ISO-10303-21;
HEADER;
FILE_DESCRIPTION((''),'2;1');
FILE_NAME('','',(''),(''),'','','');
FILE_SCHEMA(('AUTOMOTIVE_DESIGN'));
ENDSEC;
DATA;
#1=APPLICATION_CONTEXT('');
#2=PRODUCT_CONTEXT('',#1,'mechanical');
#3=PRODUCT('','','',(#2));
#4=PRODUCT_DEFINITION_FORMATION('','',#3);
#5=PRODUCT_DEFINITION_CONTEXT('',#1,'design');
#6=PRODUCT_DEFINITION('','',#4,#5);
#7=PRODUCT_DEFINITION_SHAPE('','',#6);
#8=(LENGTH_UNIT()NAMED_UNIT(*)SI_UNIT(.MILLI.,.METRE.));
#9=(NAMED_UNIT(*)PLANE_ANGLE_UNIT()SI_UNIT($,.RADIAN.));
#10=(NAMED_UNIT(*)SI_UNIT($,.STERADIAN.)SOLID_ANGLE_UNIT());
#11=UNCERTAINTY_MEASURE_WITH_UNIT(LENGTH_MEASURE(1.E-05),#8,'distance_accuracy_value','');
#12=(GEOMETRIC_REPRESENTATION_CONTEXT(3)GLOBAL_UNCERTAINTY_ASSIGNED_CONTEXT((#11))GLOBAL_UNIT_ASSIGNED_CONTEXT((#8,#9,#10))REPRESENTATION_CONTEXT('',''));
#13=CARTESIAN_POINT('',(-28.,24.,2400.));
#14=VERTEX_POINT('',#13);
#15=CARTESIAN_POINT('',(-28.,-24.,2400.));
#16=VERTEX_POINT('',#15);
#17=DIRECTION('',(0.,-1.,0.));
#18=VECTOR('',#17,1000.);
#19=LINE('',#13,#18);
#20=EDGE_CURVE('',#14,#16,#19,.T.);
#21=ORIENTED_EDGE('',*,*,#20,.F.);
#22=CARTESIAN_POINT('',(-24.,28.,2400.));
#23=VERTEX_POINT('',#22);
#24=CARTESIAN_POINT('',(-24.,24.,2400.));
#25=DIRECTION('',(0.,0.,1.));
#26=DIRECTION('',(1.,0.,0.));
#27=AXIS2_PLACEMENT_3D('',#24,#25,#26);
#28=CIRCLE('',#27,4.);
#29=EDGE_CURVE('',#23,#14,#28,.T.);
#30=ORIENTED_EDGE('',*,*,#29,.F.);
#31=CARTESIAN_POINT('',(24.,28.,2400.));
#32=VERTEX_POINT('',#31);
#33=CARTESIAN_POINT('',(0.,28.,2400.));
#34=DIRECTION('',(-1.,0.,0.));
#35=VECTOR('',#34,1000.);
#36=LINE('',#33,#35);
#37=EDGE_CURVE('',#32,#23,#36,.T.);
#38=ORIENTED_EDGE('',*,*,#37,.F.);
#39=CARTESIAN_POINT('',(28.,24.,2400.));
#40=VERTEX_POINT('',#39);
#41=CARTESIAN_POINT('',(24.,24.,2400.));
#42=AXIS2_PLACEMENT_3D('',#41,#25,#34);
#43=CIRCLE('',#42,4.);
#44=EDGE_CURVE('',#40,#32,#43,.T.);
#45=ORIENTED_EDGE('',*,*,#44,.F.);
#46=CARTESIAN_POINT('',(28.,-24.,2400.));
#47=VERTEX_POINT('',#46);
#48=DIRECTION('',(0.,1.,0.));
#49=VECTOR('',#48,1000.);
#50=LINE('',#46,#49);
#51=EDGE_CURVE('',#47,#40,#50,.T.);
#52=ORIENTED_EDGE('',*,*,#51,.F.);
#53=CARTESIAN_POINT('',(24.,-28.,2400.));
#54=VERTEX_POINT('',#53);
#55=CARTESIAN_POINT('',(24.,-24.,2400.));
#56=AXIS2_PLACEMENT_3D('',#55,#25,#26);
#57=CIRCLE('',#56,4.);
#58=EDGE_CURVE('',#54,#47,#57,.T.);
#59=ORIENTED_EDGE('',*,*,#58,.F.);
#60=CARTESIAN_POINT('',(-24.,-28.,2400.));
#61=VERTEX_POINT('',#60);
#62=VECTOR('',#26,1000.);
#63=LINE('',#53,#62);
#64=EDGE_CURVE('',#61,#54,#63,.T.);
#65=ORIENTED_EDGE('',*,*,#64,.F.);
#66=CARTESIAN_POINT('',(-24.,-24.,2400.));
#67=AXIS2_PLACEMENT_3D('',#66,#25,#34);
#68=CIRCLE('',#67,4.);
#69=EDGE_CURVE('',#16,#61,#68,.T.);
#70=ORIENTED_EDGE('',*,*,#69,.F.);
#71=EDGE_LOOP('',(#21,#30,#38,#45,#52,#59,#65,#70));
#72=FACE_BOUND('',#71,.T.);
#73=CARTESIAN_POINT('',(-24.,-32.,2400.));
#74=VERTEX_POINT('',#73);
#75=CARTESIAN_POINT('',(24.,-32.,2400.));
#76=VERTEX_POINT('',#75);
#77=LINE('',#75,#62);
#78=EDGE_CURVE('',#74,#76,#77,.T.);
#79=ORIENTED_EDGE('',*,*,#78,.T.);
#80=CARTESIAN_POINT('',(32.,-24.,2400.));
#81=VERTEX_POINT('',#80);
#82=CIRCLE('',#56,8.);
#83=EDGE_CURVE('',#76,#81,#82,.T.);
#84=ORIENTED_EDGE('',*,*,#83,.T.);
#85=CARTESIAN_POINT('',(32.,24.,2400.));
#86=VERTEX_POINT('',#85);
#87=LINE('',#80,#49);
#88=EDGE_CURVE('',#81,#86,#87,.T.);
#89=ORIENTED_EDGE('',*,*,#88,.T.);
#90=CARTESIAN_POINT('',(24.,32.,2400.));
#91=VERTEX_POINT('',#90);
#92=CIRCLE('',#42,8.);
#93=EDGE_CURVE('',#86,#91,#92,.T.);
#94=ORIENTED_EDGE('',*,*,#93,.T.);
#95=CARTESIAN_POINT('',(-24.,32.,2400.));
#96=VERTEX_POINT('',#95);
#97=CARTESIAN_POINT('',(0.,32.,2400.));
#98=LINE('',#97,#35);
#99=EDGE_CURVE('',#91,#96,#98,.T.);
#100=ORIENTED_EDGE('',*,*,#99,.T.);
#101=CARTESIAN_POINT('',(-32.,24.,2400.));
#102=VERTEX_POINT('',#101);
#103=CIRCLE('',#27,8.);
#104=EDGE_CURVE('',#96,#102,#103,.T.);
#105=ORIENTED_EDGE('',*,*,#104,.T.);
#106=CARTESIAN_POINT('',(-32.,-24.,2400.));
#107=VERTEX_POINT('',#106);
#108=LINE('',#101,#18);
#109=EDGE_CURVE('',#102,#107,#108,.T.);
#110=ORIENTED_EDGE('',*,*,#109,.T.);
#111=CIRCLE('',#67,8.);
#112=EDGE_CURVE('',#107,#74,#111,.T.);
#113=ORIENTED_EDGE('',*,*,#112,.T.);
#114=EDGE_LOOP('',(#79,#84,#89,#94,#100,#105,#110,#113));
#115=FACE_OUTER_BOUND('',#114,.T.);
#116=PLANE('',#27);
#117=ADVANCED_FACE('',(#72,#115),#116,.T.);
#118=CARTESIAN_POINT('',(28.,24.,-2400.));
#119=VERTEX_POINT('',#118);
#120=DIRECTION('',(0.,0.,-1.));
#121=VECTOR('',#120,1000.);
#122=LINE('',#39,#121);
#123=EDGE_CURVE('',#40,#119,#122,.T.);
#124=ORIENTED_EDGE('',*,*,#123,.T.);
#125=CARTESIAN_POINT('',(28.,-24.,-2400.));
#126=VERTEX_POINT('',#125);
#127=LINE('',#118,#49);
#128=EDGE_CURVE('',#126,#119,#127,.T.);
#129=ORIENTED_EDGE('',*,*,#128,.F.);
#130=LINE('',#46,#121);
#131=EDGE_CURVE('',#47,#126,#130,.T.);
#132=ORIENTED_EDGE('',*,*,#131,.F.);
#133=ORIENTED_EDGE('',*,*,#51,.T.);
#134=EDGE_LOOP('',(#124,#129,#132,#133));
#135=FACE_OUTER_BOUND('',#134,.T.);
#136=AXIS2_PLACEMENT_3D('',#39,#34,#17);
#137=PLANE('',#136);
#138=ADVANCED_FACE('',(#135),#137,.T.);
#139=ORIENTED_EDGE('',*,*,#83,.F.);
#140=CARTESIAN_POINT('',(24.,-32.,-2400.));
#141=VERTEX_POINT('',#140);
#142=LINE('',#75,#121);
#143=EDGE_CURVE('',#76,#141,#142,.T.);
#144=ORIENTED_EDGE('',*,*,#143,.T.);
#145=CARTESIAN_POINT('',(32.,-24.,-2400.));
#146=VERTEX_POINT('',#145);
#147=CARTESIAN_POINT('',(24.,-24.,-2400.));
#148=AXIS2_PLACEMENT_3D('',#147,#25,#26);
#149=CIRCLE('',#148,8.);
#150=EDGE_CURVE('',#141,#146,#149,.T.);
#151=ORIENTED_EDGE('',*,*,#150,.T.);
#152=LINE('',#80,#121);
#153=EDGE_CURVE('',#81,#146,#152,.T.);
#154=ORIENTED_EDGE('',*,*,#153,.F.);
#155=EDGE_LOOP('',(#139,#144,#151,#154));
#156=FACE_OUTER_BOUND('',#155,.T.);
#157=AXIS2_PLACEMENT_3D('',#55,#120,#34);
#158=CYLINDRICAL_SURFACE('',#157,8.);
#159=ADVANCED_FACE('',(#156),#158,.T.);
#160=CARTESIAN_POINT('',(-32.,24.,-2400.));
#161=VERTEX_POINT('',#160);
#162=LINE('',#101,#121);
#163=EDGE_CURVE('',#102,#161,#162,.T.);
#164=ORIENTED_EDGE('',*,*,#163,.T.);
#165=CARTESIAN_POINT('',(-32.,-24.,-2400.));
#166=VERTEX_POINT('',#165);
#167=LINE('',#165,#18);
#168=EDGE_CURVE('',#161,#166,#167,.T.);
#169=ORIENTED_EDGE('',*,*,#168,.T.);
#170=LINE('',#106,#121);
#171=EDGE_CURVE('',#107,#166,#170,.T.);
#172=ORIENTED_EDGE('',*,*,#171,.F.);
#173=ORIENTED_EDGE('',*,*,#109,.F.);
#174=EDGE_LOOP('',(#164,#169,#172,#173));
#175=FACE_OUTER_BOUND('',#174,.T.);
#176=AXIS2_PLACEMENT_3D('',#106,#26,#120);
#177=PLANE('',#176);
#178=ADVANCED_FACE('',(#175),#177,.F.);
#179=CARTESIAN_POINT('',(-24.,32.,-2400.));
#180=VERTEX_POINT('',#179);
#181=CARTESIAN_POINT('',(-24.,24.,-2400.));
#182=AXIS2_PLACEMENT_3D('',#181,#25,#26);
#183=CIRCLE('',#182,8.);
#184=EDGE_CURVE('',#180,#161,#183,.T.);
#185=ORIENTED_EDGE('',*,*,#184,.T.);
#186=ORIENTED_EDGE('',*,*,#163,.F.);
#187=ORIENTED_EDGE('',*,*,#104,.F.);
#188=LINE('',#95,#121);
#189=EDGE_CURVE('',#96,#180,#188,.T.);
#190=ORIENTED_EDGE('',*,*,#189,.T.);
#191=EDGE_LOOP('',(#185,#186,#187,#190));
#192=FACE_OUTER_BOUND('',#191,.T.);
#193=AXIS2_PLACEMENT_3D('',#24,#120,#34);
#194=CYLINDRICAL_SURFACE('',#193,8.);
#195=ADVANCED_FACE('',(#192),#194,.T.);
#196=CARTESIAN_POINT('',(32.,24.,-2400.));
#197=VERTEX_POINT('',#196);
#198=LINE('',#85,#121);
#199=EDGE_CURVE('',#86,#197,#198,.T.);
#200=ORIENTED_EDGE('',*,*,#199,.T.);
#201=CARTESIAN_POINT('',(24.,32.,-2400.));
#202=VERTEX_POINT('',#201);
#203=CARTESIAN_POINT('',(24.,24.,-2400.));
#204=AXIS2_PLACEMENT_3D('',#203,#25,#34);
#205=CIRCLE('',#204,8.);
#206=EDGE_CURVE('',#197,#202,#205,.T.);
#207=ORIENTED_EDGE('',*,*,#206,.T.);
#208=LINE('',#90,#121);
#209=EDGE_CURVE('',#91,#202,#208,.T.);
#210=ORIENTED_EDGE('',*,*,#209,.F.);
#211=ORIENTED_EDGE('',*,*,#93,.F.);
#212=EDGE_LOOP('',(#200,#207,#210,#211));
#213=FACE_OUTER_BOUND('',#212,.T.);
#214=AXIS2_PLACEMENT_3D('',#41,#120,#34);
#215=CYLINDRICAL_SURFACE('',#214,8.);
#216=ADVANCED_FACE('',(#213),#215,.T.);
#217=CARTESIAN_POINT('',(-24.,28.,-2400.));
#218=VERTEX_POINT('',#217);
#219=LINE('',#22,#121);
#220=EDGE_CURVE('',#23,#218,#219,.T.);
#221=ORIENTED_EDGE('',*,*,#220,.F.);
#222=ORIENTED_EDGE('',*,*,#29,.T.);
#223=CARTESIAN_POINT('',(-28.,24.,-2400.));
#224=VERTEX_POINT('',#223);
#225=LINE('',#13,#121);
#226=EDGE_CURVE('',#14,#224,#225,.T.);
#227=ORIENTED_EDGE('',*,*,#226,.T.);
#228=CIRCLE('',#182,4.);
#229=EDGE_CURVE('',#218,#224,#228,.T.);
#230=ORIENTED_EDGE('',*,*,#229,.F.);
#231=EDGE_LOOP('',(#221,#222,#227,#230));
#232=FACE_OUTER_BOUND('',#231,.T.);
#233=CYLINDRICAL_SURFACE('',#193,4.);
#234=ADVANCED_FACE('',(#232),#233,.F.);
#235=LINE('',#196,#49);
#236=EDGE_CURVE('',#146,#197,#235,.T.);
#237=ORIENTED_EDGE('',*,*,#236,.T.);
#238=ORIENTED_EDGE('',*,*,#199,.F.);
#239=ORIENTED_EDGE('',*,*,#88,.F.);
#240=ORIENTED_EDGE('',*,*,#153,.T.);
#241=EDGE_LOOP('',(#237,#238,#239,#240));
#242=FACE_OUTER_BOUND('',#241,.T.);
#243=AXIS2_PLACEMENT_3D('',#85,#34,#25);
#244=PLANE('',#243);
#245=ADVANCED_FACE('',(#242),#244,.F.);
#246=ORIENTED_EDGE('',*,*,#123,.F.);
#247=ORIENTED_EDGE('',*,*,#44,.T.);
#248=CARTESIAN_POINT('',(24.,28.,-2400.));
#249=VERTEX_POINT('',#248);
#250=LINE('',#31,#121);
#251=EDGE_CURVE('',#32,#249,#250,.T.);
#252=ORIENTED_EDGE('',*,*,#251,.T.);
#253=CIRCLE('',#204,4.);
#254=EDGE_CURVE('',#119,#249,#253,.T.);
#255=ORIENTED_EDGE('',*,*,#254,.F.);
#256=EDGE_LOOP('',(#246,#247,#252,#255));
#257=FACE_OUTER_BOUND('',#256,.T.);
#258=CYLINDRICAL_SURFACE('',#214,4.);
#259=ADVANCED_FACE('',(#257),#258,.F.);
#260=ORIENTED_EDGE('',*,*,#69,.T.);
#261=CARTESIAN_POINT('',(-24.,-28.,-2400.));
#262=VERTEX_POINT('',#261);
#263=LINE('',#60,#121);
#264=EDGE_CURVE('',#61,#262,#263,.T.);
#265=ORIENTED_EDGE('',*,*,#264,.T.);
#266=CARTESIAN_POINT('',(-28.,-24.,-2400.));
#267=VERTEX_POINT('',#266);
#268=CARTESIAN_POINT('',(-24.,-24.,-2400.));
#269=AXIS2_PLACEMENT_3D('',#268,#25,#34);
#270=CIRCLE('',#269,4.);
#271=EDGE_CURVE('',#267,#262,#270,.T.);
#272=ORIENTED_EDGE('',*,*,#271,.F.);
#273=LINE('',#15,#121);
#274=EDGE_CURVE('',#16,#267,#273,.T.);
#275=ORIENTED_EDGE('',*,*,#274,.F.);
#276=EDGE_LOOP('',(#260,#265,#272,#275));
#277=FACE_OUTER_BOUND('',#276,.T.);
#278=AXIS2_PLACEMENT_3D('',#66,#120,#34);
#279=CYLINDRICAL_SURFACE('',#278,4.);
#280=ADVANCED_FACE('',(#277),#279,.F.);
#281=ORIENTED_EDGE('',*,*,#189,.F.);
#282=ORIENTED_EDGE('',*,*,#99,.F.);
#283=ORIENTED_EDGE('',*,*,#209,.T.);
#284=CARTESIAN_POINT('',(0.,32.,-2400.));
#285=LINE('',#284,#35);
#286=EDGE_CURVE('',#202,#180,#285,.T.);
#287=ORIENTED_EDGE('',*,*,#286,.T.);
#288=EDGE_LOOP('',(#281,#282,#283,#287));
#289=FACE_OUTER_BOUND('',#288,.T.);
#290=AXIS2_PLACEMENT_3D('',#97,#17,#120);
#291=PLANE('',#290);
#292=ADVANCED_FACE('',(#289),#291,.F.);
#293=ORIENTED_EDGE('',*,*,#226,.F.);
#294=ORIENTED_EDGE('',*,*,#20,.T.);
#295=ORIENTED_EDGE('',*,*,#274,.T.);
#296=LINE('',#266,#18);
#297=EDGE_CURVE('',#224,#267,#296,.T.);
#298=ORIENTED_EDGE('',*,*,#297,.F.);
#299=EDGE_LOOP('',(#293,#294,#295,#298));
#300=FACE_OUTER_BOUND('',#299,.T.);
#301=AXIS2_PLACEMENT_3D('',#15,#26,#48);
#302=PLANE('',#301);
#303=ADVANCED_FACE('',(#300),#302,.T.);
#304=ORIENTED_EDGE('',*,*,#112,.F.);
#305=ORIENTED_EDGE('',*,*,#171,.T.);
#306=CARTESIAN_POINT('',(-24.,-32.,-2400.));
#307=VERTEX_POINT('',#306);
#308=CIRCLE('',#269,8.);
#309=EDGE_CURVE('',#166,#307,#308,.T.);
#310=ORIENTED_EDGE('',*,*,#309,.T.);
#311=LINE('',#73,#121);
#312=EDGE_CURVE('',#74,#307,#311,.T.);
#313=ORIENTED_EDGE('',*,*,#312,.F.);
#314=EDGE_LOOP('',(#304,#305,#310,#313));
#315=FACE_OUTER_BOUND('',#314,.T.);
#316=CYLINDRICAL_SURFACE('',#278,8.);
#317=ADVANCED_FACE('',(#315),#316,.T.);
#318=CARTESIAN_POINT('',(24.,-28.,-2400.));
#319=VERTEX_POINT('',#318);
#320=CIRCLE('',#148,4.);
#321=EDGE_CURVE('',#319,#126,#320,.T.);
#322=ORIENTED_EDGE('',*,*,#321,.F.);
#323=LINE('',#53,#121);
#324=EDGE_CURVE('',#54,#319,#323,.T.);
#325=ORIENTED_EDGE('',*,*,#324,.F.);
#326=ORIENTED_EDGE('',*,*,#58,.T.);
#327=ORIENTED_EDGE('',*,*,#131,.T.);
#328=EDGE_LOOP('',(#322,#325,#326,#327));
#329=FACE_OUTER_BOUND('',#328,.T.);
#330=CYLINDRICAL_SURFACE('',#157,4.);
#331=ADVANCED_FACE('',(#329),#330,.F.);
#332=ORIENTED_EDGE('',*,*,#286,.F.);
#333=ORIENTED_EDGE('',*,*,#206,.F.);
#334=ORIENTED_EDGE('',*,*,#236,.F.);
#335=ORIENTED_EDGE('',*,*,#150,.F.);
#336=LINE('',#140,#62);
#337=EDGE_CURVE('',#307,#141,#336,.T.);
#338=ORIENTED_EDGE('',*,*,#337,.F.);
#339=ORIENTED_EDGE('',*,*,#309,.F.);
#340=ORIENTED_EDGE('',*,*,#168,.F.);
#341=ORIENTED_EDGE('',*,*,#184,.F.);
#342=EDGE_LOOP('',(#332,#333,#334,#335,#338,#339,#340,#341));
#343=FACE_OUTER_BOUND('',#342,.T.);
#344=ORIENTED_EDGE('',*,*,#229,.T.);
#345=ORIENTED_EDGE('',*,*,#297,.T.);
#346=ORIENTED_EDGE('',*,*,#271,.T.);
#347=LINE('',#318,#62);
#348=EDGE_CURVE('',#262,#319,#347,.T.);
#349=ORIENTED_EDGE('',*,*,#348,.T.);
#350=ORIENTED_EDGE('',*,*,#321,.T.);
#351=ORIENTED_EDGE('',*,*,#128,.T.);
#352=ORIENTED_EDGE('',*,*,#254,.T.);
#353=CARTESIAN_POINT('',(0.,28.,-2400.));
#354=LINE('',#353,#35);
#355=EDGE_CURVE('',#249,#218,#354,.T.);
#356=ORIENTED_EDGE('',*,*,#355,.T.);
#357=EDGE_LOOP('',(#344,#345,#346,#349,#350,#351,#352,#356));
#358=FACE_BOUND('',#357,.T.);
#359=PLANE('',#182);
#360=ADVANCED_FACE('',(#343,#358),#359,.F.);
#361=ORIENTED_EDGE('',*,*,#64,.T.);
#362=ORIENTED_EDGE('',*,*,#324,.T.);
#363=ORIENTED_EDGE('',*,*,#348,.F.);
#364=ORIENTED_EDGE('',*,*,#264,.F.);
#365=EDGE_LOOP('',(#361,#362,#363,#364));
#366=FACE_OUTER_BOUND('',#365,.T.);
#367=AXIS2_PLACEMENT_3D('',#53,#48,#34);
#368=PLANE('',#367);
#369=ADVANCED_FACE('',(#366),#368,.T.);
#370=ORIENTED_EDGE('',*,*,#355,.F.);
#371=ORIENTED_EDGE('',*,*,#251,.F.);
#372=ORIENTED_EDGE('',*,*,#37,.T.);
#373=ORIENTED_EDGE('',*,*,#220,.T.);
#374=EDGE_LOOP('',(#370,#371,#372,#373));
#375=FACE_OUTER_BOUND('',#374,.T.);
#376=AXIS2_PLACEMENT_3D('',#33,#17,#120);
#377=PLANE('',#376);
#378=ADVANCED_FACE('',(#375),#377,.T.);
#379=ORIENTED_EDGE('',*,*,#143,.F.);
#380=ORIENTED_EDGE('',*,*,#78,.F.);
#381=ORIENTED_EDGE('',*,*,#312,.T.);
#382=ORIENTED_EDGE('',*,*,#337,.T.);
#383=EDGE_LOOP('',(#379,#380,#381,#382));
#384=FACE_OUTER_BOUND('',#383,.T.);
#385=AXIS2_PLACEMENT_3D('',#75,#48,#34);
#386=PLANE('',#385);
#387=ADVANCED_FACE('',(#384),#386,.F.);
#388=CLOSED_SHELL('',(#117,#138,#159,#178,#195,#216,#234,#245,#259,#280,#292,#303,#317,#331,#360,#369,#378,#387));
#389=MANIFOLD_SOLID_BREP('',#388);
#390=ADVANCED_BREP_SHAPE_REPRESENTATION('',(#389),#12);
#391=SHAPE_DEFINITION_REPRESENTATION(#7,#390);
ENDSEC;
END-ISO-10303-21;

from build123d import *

# Parameters (mm, degrees)
BOSS_EXTRUDE_1_DEPTH = 2400


with BuildPart() as part:
    # Sketch 1 → Boss-Extrude 1 (new, symmetric)
    with BuildSketch(Plane.XY):
        with BuildLine():
            Line((0, 32), (-24, 32))
            ThreePointArc((-24, 32), (-29.656854249, 29.656854249), (-32, 24))
            Line((-32, 24), (-32, 0))
            Line((-32, 0), (-32, -24))
            ThreePointArc((-32, -24), (-29.656854249, -29.656854249), (-24, -32))
            Line((-24, -32), (24, -32))
            ThreePointArc((24, -32), (29.656854249, -29.656854249), (32, -24))
            Line((32, -24), (32, 0))
            Line((32, 0), (32, 24))
            ThreePointArc((32, 24), (29.656854249, 29.656854249), (24, 32))
            Line((24, 32), (0, 32))
        make_face()
        with BuildLine():
            Line((0, 28), (-24, 28))
            ThreePointArc((-24, 28), (-26.828427125, 26.828427125), (-28, 24))
            Line((-28, 24), (-28, 0))
            Line((-28, 0), (-28, -24))
            ThreePointArc((-28, -24), (-26.828427125, -26.828427125), (-24, -28))
            Line((-24, -28), (24, -28))
            ThreePointArc((24, -28), (26.828427125, -26.828427125), (28, -24))
            Line((28, -24), (28, 0))
            Line((28, 0), (28, 24))
            ThreePointArc((28, 24), (26.828427125, 26.828427125), (24, 28))
            Line((24, 28), (0, 28))
        make_face(mode=Mode.SUBTRACT)
    extrude(amount=BOSS_EXTRUDE_1_DEPTH, both=True)


solid = part.part
